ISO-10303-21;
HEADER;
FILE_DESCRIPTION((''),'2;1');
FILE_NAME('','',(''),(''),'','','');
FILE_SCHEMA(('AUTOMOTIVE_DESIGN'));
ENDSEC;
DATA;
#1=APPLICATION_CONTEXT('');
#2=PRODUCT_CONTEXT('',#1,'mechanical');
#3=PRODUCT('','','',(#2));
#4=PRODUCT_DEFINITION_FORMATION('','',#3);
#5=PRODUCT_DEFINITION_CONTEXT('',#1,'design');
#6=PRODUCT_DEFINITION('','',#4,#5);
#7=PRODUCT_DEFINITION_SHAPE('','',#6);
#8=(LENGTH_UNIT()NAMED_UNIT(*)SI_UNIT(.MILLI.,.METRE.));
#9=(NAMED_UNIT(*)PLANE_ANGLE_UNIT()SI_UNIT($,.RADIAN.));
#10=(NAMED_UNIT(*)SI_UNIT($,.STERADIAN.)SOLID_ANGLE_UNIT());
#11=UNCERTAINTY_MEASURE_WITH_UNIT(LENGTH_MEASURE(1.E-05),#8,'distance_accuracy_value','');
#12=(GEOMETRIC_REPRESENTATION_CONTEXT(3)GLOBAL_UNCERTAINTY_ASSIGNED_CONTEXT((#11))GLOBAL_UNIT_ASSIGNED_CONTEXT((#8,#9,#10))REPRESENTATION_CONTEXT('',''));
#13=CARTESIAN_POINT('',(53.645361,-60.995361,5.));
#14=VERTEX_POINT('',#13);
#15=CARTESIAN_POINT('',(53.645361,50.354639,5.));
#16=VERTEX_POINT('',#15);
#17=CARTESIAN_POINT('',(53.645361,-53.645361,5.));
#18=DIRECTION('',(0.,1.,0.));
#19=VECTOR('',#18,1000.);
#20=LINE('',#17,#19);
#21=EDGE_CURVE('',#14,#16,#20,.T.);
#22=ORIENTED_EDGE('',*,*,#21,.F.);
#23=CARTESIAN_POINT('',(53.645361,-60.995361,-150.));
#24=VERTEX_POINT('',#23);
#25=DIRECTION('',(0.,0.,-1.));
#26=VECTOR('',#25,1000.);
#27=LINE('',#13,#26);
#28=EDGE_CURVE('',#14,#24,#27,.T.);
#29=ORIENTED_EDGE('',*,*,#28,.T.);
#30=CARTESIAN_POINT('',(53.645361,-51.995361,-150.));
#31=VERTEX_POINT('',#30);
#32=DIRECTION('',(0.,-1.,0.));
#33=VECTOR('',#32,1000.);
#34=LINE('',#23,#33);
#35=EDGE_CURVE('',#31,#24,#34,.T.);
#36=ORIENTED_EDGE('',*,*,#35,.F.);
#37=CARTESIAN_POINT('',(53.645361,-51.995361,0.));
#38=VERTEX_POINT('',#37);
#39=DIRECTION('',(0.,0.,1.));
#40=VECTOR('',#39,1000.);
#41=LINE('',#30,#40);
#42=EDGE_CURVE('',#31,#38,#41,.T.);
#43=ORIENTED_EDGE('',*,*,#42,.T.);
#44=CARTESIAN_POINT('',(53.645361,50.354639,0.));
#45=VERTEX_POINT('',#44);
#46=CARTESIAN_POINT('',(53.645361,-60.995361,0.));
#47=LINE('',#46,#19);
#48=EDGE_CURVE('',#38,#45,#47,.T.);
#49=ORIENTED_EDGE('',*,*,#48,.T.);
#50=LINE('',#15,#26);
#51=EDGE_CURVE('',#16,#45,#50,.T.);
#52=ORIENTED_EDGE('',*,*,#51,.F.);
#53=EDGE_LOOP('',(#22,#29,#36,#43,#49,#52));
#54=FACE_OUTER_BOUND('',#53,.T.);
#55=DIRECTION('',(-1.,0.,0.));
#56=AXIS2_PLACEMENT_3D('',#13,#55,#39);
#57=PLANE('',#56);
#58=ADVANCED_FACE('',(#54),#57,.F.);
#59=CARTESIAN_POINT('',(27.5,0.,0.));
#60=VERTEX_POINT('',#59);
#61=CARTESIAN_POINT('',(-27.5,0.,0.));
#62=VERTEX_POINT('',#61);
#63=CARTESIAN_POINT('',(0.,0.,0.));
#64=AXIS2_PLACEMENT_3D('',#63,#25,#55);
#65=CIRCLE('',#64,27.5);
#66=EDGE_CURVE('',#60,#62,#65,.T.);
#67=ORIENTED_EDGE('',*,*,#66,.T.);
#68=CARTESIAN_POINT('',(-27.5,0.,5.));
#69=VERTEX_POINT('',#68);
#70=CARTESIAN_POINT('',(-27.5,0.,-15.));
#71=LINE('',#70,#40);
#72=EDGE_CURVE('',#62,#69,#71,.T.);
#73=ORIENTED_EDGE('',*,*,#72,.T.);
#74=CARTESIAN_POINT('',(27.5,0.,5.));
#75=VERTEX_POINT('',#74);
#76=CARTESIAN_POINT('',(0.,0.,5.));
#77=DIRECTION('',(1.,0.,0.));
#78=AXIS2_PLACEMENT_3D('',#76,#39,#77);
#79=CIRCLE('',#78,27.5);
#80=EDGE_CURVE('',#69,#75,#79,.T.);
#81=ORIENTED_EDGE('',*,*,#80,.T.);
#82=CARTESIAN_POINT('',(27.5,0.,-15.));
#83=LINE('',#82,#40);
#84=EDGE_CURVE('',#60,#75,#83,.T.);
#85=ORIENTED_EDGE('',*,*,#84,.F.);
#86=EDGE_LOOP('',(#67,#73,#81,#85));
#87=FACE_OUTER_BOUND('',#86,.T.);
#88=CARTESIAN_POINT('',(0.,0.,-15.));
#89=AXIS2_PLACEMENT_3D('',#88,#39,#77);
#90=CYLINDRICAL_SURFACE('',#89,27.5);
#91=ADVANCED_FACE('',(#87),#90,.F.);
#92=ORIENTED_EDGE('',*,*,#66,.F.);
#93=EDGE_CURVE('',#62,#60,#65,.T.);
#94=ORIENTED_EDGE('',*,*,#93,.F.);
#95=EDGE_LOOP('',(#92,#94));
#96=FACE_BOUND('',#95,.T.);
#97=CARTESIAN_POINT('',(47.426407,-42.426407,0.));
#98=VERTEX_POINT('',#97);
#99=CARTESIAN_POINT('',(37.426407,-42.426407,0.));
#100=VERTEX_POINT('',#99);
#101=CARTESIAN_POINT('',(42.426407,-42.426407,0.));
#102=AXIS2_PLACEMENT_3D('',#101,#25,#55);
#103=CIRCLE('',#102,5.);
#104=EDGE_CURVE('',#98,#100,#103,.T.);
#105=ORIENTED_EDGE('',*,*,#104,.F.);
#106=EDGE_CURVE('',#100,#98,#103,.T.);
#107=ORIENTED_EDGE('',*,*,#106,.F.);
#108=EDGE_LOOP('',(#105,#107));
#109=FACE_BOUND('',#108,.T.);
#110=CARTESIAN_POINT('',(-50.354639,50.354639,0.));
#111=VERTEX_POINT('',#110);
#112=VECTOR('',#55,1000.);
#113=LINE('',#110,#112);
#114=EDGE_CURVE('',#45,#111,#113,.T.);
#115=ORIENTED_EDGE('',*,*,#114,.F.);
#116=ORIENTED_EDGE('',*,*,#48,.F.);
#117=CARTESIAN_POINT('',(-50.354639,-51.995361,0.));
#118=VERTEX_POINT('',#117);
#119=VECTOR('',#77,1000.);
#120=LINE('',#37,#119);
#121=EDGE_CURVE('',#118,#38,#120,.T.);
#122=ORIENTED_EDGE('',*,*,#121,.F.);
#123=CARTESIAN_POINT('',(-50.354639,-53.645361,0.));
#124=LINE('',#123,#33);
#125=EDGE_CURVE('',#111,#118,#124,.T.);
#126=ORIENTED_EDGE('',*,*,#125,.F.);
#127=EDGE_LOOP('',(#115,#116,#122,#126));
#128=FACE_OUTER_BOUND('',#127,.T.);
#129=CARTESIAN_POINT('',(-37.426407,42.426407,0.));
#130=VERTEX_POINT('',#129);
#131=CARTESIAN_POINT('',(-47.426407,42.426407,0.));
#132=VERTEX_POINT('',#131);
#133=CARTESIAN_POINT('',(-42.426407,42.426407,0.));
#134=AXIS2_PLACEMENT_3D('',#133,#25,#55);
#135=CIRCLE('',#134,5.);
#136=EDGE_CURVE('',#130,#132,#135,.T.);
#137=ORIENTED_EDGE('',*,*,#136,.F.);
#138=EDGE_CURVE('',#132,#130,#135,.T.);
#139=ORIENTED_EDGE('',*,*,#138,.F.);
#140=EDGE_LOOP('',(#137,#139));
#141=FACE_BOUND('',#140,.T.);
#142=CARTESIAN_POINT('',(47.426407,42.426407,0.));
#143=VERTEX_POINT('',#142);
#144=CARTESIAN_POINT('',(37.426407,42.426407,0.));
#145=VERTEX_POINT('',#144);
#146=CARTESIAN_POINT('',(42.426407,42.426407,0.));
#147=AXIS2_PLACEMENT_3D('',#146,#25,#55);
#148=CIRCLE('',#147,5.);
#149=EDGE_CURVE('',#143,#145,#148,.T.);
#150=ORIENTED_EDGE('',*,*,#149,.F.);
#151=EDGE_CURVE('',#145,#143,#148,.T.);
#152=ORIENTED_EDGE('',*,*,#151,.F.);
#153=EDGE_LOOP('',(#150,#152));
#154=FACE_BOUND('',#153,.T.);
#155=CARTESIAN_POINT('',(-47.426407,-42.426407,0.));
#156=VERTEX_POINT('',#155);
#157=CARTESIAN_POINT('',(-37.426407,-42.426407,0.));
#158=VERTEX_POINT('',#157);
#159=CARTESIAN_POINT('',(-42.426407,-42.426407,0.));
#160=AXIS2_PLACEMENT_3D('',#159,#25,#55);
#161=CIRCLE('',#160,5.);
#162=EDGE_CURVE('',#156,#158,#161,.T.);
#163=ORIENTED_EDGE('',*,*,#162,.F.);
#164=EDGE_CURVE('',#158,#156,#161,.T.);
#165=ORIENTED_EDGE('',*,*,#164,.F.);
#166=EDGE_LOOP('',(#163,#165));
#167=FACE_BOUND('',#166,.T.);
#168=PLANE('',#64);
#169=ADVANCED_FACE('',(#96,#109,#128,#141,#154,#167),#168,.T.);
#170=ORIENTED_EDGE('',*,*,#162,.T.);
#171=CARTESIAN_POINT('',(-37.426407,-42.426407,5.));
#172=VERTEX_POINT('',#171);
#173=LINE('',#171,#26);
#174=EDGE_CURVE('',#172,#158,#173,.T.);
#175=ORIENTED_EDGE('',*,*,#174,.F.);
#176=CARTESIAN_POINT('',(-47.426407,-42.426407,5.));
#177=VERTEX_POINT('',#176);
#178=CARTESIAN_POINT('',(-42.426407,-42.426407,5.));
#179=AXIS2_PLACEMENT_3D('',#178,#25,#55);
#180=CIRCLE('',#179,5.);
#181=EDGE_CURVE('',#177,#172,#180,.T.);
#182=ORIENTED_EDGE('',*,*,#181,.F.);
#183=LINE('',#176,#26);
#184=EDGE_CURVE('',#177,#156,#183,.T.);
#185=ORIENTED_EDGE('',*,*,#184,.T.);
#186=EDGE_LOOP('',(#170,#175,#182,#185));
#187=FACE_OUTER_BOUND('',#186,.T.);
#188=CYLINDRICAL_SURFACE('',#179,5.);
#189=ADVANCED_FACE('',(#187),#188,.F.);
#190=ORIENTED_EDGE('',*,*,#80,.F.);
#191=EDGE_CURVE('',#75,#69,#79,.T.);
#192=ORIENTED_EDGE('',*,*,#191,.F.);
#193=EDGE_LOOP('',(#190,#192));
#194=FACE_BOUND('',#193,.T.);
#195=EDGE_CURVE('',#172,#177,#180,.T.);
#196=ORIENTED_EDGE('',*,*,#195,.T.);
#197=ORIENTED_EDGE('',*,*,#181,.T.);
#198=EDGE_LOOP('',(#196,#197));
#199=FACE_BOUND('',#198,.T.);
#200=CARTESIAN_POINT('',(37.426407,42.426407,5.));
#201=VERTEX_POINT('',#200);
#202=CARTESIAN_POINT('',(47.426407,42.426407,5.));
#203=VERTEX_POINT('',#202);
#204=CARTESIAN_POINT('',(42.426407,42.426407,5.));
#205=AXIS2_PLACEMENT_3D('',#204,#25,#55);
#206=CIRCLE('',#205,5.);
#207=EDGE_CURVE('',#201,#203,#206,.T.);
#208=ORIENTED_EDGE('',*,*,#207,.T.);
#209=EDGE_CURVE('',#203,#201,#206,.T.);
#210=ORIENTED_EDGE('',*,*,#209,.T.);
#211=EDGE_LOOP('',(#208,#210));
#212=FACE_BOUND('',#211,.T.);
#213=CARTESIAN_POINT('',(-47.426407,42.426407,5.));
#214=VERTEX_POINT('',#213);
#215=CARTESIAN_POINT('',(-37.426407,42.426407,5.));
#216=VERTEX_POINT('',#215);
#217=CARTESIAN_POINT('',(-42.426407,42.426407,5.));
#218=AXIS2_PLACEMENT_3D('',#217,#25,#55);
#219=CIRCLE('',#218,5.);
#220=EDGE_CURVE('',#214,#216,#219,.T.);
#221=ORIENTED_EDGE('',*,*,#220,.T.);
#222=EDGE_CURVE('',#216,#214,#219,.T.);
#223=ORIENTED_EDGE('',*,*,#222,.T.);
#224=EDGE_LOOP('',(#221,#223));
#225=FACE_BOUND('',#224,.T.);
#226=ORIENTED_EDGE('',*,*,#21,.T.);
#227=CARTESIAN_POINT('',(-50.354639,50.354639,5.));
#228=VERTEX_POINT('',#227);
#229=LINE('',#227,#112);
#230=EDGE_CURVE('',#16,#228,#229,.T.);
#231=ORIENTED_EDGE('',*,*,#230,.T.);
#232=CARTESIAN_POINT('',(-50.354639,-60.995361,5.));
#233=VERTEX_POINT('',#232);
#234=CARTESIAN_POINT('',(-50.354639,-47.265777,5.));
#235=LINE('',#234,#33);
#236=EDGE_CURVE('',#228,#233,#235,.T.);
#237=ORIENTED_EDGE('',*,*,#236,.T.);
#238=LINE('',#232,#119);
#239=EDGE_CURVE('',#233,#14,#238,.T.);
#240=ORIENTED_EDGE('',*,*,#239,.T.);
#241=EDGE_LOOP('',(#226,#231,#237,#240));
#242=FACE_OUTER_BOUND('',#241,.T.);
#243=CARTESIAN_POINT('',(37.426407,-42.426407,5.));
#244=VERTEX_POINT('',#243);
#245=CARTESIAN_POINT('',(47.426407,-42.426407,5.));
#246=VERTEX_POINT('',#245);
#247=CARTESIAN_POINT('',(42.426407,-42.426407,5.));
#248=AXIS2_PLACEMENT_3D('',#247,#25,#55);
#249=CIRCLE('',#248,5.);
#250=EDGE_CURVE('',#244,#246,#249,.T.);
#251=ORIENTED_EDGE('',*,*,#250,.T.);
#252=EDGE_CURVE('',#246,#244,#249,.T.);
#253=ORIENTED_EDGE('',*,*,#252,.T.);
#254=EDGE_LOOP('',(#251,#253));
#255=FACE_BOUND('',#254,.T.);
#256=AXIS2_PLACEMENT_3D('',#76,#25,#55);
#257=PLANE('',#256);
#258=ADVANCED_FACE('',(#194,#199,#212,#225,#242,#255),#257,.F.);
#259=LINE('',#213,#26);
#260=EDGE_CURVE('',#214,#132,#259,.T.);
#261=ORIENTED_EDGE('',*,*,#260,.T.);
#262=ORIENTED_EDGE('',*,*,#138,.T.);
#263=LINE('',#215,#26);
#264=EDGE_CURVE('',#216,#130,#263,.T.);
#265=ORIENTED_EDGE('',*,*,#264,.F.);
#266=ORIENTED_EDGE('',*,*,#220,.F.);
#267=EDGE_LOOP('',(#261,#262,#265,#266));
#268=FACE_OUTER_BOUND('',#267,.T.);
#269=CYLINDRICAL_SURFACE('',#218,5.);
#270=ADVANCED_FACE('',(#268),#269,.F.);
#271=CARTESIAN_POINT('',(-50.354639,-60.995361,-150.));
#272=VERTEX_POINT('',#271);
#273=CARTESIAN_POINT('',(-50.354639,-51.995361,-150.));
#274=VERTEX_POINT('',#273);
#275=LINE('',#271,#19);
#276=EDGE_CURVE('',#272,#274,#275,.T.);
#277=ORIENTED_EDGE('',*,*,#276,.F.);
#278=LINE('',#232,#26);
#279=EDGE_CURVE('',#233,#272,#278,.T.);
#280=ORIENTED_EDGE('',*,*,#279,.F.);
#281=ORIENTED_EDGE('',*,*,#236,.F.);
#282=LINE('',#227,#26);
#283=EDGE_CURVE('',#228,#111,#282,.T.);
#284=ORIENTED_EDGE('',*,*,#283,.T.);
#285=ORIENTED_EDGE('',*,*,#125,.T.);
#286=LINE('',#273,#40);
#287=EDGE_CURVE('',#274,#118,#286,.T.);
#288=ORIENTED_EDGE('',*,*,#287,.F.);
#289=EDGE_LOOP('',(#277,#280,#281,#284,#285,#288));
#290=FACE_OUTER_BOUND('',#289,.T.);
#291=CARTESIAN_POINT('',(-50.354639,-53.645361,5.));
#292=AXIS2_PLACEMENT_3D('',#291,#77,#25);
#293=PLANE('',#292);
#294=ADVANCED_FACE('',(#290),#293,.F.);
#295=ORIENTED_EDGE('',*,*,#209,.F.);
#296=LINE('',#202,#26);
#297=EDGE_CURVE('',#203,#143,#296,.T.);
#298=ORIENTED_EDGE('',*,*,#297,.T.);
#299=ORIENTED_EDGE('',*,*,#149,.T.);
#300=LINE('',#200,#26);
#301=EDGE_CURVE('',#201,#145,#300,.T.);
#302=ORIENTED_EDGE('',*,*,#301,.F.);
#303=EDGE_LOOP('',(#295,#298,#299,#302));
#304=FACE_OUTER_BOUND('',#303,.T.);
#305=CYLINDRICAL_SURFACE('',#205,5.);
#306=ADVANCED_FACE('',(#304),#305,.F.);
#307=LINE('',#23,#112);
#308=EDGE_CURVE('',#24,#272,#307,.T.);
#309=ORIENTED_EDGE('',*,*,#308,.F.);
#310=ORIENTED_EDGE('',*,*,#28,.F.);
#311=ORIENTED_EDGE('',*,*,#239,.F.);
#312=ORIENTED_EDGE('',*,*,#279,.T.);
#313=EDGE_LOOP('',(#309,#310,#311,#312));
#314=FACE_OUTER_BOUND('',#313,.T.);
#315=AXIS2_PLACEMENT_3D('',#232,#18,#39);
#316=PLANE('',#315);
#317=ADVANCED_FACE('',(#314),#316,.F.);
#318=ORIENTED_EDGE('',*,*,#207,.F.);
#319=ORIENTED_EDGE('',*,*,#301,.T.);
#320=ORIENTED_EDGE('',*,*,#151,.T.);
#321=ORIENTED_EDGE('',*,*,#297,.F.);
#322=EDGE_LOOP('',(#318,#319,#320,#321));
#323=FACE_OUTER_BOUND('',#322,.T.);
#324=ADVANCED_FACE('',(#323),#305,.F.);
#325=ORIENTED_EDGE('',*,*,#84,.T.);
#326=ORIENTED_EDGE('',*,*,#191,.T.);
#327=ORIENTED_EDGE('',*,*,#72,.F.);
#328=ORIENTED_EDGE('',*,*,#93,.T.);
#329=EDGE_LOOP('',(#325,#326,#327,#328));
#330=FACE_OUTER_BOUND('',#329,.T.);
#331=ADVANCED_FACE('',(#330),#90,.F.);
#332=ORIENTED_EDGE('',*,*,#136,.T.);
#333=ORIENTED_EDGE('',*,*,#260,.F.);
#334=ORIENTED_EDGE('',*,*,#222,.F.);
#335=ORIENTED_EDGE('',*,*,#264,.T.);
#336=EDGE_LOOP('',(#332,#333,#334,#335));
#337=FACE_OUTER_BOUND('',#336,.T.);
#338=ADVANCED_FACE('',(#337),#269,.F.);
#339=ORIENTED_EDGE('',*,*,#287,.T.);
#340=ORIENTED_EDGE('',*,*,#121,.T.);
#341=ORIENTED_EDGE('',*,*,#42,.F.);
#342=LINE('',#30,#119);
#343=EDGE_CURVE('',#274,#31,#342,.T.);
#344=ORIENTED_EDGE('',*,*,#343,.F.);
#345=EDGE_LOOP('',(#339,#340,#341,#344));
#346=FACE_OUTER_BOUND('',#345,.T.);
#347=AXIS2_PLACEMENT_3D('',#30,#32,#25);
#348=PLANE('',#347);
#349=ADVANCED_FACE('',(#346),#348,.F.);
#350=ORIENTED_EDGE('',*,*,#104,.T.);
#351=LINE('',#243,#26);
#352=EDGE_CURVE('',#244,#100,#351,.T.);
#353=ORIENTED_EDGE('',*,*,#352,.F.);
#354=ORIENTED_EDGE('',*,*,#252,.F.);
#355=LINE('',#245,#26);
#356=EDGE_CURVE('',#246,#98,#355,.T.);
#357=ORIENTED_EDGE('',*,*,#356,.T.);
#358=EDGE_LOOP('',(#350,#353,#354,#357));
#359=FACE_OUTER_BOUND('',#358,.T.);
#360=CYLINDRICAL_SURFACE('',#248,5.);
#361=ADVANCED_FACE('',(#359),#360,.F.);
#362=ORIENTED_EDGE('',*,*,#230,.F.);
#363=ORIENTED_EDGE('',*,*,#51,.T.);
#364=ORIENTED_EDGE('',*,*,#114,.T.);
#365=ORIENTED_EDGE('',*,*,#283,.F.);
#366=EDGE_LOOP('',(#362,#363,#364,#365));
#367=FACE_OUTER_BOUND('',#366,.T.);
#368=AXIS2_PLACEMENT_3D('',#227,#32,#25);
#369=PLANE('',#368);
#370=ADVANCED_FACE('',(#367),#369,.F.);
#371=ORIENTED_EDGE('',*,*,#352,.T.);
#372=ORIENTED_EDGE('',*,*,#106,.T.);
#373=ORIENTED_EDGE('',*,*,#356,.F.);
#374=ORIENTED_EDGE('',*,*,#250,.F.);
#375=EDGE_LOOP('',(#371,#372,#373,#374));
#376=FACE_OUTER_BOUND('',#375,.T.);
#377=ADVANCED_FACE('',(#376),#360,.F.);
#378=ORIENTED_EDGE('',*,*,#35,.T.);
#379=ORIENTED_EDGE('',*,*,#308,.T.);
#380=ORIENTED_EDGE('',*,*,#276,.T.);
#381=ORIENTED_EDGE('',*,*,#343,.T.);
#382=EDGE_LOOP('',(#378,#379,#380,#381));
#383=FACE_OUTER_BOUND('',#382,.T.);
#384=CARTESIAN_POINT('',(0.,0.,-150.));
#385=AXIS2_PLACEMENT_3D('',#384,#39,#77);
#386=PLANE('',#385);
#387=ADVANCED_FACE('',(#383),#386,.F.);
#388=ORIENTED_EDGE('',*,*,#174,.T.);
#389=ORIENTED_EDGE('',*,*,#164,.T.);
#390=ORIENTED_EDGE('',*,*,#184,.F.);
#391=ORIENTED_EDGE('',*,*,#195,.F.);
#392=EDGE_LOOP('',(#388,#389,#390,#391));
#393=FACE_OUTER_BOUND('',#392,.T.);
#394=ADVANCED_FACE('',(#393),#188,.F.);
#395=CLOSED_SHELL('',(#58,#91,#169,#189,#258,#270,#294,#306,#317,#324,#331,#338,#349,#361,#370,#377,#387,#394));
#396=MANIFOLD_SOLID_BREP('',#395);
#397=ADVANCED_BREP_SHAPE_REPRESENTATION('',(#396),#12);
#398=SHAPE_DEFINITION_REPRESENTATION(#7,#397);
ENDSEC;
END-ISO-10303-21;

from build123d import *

# Parameters (mm, degrees)
EXTRUDE_1_DEPTH          = 5
SKETCH_4_R               = 27.5
CUT_EXTRUDE_4_DEPTH      = 20
SKETCH_5_W               = 104
SKETCH_5_H               = 9
EXTRUDE_2_DEPTH          = 150
CUT_EXTRUDE_5_DEPTH      = 171.582117426
CUT_EXTRUDE_5_DEPTH_BACK = 171.582117426
SKETCH_6_R               = 5


with BuildPart() as part:
    # 草图1 → 凸台-拉伸1 (new body)
    with BuildSketch(Plane.XY):
        Polygon((-50.354639151, -47.265777393), (-50.354639151, -53.645360849), (-50.354639151, -60.995360849), (53.645360849, -60.995360849), (53.645360849, -53.645360849), (53.645360849, 50.354639151), (-50.354639151, 50.354639151), align=None)
    extrude(amount=EXTRUDE_1_DEPTH)

    # 草图4 → 切除-拉伸4 (cut)
    with BuildSketch(Plane.XY.offset(5)):
        Circle(SKETCH_4_R)
    extrude(amount=-CUT_EXTRUDE_4_DEPTH, mode=Mode.SUBTRACT)

    # 草图5 → 凸台-拉伸2 (add)
    with BuildSketch(Plane(origin=(0, 0, 0), x_dir=(-1, 0, 0), z_dir=(0, 0, -1))):
        with Locations((-1.645360849, -56.495360849)):
            Rectangle(SKETCH_5_W, SKETCH_5_H)
    extrude(amount=EXTRUDE_2_DEPTH)

    # 草图6 → 切除-拉伸5 (cut, two sides: drawn at the far end of the back side and taken through both)
    with BuildSketch(Plane(origin=(0, 0, 0), x_dir=(-1, 0, 0), z_dir=(0, 0, -1)).offset(-CUT_EXTRUDE_5_DEPTH_BACK)):
        with Locations((-42.426406871, 42.426406871)):
            Circle(SKETCH_6_R)
        with Locations((42.426406871, 42.426406871)):
            Circle(SKETCH_6_R)
        with Locations((42.426406871, -42.426406871)):
            Circle(SKETCH_6_R)
        with Locations((-42.426406871, -42.426406871)):
            Circle(SKETCH_6_R)
    extrude(amount=CUT_EXTRUDE_5_DEPTH + CUT_EXTRUDE_5_DEPTH_BACK, mode=Mode.SUBTRACT)


solid = part.part
